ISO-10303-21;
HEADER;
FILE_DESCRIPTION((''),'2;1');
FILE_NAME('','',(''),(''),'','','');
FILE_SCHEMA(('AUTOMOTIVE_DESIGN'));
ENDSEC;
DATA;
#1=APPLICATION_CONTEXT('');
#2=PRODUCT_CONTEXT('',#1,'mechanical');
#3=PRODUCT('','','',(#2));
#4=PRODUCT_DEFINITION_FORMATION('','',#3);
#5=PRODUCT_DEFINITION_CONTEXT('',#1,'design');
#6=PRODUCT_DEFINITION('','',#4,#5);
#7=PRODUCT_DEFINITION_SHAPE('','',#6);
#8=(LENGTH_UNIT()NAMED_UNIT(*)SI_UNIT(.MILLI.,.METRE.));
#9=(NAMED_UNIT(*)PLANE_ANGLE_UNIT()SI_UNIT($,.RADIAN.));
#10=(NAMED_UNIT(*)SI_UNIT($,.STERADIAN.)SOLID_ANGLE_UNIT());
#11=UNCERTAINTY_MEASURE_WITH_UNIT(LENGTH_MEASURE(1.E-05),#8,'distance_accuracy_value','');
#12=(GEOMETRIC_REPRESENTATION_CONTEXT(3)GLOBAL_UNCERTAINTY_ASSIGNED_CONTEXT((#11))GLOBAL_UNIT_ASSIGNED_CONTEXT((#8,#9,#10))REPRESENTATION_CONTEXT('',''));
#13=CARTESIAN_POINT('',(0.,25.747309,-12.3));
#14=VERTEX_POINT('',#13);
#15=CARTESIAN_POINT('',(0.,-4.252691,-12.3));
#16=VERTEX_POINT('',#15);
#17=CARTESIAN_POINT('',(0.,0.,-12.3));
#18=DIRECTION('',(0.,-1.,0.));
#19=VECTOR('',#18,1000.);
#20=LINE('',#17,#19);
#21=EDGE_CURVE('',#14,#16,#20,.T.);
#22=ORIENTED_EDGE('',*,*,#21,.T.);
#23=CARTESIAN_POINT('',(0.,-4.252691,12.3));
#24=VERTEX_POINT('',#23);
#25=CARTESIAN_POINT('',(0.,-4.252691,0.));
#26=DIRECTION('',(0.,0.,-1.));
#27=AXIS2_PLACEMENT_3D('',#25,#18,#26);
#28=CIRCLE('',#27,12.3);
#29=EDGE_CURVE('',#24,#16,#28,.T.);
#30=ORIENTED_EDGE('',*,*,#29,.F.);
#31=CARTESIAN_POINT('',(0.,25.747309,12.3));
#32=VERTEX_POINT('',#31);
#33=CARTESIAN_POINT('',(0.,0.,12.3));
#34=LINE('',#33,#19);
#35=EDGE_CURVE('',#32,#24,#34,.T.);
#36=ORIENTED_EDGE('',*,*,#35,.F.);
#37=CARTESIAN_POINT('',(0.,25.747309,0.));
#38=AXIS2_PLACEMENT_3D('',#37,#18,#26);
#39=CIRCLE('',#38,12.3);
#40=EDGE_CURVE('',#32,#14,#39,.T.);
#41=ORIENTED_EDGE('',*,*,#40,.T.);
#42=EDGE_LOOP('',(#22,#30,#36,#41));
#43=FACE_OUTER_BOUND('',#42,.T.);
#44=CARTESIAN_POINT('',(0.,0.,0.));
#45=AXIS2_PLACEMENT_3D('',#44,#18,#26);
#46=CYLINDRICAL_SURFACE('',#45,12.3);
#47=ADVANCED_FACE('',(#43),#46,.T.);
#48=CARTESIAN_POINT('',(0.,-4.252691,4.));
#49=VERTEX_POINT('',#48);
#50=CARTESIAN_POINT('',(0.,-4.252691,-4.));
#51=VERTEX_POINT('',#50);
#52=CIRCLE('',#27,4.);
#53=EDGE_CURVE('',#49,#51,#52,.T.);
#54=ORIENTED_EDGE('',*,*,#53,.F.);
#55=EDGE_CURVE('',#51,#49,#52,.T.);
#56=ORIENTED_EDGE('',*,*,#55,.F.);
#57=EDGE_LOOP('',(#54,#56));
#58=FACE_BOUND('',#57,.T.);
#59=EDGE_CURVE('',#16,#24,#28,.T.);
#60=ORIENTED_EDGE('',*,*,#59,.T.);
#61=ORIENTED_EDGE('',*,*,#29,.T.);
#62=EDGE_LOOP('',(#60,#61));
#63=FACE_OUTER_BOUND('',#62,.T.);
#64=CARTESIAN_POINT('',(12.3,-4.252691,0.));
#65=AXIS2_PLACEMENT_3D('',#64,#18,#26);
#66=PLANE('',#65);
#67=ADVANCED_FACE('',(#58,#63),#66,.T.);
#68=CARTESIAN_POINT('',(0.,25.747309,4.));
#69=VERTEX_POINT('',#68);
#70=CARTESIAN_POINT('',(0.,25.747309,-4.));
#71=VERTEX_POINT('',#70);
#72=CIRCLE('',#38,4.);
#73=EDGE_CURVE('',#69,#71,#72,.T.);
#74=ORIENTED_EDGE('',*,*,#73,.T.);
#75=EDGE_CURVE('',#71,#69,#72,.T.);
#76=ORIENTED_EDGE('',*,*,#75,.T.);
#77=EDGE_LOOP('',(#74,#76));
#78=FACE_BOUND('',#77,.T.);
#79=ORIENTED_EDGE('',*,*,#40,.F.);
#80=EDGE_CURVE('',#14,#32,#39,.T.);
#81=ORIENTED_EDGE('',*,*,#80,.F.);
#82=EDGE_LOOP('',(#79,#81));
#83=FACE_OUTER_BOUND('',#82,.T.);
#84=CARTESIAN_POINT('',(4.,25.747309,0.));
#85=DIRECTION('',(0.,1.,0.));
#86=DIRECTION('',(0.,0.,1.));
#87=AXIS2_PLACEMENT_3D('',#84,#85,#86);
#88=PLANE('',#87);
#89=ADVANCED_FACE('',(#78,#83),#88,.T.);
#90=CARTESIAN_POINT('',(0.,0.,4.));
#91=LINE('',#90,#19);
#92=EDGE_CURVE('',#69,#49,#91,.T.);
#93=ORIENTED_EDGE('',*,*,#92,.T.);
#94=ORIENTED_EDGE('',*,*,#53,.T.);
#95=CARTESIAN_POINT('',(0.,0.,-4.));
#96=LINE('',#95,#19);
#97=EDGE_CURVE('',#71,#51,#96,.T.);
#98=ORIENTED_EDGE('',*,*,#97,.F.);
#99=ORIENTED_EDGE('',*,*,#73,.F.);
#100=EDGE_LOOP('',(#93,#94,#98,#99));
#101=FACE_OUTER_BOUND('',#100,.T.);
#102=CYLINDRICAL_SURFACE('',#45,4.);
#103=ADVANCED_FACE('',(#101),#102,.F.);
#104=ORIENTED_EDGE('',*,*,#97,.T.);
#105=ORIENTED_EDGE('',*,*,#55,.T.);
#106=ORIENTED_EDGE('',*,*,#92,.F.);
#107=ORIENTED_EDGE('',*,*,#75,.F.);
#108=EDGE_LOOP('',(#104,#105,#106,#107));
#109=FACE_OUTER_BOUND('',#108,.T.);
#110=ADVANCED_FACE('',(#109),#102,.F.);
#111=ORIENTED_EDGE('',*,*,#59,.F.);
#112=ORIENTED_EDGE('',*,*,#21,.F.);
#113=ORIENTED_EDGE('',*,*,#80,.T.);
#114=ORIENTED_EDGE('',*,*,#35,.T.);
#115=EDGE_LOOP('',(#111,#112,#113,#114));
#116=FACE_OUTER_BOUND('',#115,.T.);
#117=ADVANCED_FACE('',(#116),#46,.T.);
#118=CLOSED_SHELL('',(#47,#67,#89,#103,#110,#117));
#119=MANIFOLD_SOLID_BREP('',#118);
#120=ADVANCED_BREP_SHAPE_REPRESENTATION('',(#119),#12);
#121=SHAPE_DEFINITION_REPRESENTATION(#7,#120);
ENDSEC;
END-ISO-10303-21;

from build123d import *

# Parameters (mm, degrees)
SKETCH_1_W = 8.3
SKETCH_1_H = 30


with BuildPart() as part:
    # 草图1 → 旋转1 (revolve)
    with BuildSketch(Plane.XY, mode=Mode.PRIVATE) as revolve_1_sk:
        with Locations((8.15, 10.747308607)):
            Rectangle(SKETCH_1_W, SKETCH_1_H)
    revolve(revolve_1_sk.sketch.rotate(Axis((0, 0, 0), (0, 1, 0)), 90), axis=Axis((0, 0, 0), (0, 1, 0)))


solid = part.part
